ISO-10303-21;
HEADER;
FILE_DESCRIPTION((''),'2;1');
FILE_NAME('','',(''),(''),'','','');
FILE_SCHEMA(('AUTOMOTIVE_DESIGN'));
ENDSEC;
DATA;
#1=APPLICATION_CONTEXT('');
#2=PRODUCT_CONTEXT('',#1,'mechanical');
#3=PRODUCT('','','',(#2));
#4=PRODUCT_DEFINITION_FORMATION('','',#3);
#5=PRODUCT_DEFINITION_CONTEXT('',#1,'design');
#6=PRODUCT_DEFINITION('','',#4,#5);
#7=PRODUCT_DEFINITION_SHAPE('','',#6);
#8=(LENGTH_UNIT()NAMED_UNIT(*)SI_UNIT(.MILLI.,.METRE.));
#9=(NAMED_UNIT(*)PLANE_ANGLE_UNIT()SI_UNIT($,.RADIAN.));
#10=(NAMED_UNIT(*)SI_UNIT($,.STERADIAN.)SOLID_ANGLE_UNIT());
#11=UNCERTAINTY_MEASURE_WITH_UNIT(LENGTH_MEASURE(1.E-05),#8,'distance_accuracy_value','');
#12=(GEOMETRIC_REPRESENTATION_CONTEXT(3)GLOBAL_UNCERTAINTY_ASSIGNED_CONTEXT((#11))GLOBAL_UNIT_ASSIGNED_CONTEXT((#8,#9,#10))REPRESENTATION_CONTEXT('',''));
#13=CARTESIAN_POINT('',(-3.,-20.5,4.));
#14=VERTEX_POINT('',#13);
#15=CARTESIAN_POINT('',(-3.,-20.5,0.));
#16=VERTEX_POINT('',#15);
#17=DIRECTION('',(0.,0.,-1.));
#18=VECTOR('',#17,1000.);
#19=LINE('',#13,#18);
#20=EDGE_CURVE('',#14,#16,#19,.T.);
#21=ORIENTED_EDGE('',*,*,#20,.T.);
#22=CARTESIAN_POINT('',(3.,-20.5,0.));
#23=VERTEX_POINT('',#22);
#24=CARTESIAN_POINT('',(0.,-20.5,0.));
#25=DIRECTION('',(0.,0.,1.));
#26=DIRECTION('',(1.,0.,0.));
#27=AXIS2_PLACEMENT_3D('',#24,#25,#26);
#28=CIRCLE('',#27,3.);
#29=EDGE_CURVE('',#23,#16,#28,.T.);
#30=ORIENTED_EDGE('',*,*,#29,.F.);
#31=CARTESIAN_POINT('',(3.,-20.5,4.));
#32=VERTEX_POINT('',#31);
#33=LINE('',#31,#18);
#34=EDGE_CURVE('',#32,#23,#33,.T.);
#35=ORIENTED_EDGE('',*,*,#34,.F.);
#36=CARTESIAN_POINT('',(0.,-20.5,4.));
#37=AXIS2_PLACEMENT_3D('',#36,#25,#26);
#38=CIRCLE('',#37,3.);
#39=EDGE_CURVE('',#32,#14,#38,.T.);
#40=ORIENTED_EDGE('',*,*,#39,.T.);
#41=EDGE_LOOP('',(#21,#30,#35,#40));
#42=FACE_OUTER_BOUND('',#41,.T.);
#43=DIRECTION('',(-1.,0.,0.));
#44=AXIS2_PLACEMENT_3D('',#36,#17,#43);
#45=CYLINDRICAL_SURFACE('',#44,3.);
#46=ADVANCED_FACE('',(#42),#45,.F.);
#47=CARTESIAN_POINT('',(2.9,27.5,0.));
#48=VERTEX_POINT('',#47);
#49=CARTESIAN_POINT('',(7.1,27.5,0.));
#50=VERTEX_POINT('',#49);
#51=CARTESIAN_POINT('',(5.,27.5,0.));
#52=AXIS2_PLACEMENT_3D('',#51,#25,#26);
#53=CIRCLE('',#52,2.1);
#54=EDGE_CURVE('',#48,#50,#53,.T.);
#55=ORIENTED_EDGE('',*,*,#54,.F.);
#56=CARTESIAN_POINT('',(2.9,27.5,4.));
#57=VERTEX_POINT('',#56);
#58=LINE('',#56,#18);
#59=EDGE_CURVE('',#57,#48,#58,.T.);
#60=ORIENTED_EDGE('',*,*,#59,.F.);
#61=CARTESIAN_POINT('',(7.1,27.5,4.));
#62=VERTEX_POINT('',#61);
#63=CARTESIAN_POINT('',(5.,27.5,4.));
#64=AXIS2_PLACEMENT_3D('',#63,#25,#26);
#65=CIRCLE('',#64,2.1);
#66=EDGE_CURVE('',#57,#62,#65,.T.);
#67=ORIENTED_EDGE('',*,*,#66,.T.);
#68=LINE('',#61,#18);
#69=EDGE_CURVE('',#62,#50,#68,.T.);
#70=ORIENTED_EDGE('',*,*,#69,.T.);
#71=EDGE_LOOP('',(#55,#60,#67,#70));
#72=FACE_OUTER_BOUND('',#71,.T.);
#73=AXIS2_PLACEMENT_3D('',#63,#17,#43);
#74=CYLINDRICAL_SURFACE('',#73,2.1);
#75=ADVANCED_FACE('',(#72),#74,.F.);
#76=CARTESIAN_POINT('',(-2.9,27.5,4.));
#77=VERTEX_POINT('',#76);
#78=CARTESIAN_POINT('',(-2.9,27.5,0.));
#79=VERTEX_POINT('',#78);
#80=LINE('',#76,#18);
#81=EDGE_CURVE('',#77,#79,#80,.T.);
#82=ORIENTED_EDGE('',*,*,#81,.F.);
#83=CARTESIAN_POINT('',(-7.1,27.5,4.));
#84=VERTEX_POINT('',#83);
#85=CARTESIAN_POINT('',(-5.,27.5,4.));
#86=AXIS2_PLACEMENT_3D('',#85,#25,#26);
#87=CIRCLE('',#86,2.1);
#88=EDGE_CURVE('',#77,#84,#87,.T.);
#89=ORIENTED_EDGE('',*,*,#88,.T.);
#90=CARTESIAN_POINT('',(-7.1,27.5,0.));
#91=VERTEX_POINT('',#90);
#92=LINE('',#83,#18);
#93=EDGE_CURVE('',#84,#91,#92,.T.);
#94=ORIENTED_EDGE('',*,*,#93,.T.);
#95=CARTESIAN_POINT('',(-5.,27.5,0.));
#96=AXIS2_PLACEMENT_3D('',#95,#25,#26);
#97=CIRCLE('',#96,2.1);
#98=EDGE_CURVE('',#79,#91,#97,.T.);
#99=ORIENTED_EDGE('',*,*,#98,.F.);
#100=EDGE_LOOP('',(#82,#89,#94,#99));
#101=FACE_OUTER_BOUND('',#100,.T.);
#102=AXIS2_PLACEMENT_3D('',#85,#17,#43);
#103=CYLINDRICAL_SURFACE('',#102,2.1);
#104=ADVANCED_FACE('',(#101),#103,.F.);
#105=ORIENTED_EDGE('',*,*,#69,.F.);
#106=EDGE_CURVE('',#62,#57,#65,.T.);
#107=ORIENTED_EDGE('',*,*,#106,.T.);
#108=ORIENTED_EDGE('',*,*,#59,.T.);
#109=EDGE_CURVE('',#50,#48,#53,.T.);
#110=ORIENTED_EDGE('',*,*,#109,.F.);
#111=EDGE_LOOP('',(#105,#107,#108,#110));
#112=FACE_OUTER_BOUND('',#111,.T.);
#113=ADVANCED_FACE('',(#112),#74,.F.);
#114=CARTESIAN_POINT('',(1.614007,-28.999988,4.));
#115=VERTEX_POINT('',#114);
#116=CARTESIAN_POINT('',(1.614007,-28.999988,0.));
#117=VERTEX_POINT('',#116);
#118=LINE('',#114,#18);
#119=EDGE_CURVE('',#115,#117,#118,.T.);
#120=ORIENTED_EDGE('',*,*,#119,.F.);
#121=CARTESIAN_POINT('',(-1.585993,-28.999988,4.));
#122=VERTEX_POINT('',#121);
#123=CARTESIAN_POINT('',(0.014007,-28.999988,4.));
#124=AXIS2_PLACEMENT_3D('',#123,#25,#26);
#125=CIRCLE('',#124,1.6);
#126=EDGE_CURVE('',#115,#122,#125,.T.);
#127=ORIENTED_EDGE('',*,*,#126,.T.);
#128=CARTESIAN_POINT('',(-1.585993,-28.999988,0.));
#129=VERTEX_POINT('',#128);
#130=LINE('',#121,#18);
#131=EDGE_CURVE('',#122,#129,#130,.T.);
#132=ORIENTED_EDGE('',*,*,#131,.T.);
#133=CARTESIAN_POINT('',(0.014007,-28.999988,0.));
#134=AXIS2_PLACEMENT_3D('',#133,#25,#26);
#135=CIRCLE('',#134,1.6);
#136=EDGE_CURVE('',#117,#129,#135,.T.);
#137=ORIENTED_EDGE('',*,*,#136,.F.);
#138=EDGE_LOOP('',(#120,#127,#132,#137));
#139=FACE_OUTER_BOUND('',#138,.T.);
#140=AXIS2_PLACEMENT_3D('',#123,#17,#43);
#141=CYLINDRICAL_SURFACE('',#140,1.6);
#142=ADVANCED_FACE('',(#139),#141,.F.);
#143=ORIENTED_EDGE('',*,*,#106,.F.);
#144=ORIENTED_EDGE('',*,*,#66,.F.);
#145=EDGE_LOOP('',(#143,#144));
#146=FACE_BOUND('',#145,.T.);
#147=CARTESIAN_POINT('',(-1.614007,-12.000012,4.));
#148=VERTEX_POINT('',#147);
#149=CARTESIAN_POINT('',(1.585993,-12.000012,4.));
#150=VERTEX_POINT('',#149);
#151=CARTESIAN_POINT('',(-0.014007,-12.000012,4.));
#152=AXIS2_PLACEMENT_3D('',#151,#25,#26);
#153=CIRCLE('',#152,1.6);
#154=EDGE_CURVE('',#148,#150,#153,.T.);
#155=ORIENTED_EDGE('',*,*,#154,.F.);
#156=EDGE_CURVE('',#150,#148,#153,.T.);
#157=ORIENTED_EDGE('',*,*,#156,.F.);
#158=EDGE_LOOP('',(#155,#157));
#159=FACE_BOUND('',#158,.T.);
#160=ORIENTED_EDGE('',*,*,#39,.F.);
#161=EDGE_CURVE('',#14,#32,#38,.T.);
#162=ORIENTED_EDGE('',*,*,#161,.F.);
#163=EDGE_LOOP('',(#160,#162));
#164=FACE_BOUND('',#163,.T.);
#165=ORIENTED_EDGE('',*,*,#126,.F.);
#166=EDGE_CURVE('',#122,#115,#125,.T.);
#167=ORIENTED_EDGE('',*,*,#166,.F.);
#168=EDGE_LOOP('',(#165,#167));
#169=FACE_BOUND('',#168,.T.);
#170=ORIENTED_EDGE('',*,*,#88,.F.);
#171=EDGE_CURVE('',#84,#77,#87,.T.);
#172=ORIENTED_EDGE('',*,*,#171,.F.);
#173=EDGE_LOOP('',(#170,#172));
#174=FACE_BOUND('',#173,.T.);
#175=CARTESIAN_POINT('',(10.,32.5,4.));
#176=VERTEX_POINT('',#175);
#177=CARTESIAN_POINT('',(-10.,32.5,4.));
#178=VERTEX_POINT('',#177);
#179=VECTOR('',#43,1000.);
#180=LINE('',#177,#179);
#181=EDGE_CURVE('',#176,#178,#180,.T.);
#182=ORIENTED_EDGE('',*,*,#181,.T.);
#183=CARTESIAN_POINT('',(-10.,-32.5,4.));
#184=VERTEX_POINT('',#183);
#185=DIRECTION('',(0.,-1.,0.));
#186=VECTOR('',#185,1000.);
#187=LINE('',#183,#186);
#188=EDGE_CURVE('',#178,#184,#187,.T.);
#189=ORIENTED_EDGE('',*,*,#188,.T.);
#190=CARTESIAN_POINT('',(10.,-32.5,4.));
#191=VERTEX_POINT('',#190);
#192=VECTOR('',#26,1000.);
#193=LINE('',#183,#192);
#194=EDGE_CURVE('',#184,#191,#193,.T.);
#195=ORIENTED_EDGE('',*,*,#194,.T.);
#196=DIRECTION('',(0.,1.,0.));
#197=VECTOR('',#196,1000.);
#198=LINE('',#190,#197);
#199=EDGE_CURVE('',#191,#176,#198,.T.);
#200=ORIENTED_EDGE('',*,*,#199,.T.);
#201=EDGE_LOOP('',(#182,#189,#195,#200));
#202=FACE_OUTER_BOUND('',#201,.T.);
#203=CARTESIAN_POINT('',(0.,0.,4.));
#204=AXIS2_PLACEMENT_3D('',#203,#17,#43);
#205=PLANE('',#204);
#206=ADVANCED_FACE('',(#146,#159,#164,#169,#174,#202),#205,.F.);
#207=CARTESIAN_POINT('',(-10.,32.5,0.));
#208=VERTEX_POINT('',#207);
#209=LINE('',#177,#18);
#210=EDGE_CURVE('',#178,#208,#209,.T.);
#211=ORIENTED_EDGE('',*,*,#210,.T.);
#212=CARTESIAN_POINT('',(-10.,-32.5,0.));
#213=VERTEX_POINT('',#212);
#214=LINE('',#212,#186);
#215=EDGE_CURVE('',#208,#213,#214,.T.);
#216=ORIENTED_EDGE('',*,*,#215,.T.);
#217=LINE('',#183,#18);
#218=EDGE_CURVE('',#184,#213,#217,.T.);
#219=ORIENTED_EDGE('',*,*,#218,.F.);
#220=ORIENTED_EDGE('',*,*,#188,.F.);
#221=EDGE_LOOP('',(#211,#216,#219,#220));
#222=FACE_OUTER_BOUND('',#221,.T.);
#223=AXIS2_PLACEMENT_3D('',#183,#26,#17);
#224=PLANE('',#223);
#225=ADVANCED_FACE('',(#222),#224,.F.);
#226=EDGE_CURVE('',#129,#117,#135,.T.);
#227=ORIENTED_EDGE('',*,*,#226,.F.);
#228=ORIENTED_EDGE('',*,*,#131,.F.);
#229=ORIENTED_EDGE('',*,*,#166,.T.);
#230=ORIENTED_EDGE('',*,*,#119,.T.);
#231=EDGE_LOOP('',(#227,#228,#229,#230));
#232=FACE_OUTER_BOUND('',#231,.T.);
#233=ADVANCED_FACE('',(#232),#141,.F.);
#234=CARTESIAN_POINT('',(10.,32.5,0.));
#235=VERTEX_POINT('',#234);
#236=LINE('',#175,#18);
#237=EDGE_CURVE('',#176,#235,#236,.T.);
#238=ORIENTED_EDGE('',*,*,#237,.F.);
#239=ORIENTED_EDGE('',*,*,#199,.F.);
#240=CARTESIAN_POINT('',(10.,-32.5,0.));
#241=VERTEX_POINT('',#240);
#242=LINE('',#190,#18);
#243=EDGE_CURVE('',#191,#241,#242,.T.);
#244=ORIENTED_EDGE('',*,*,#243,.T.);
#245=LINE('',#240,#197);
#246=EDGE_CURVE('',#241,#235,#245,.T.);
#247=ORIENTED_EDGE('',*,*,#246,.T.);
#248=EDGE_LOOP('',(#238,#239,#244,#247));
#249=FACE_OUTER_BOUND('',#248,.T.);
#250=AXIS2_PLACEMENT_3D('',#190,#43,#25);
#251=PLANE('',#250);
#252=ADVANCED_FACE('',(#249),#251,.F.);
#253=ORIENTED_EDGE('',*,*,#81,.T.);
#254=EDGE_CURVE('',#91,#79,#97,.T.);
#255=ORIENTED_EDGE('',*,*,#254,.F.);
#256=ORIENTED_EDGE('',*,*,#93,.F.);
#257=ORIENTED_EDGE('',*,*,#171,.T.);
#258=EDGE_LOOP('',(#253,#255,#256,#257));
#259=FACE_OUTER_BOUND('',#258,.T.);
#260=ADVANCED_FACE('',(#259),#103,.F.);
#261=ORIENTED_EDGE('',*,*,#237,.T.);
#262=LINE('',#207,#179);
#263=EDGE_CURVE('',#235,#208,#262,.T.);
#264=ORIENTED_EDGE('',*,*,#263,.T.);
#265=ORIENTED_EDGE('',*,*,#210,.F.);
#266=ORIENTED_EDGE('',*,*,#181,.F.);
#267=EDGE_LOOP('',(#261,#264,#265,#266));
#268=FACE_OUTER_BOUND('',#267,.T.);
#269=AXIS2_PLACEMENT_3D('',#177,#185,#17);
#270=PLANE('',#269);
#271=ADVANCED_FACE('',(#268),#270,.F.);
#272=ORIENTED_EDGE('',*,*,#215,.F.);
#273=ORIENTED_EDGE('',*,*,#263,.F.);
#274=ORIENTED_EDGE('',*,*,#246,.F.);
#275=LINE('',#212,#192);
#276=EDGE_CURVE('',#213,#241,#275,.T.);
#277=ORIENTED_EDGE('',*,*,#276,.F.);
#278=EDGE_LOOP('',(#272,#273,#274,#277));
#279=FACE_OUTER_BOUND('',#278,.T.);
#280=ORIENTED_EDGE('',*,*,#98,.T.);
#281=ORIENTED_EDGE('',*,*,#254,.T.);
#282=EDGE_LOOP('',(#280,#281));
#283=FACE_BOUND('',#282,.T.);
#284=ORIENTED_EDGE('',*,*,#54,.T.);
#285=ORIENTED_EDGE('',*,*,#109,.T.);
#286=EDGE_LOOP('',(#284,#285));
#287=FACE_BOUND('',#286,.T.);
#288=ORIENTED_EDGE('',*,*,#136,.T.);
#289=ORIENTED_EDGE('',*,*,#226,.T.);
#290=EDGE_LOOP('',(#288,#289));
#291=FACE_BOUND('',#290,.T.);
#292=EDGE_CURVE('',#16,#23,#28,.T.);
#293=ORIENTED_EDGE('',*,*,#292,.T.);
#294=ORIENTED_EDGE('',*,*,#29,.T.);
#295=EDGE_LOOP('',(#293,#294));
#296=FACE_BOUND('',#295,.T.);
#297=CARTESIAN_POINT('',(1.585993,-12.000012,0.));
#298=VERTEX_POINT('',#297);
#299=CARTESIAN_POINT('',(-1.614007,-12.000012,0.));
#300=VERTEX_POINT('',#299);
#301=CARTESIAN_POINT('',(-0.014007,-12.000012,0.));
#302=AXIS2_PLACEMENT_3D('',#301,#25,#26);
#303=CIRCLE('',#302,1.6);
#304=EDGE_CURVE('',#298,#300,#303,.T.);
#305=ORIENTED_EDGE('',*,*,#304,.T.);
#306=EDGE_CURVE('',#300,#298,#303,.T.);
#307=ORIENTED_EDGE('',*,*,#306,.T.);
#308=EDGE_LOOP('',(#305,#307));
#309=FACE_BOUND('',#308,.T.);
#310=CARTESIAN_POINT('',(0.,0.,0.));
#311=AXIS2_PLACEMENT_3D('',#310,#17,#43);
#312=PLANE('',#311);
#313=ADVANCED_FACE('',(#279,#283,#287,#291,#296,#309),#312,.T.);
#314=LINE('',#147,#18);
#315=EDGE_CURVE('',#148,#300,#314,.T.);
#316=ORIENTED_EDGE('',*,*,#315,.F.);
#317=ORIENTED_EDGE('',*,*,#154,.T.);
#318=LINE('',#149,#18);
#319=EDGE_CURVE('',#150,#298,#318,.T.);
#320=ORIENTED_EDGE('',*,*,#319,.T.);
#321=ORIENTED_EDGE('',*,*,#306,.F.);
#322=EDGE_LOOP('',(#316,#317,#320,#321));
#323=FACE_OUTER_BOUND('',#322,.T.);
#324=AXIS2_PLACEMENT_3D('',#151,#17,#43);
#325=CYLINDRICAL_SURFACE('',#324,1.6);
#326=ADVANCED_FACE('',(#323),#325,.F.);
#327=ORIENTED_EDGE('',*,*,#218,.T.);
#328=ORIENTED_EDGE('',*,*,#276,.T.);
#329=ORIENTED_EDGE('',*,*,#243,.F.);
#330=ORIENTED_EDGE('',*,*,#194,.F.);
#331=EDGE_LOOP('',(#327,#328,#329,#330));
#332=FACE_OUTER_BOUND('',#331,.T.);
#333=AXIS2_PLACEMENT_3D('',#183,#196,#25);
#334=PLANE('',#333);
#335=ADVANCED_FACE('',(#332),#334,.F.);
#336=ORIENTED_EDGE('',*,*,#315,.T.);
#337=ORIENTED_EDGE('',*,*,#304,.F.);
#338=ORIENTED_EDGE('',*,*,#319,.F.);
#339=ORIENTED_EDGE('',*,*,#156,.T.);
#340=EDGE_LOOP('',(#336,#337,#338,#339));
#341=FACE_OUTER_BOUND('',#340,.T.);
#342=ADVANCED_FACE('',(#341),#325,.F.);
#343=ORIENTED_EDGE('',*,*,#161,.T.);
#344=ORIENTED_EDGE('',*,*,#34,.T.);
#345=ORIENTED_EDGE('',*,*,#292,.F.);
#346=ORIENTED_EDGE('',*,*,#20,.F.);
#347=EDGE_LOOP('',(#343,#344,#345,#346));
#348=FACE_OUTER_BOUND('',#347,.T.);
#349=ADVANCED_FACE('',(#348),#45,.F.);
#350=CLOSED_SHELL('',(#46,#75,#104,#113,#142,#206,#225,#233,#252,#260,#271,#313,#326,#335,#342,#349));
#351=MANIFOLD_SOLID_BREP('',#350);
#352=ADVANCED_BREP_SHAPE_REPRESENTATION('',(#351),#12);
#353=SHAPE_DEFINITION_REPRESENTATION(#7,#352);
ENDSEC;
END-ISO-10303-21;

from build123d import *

# Parameters (mm, degrees)
SKETCH1_W           = 20
SKETCH1_H           = 65
SKETCH1_R           = 2.1
SKETCH1_R_2         = 3
SKETCH1_R_3         = 1.6
BOSS_EXTRUDE1_DEPTH = 4


with BuildPart() as part:
    # Sketch1 → Boss-Extrude1 (new body)
    with BuildSketch(Plane.XY):
        Rectangle(SKETCH1_W, SKETCH1_H)
        with Locations((-5, 27.5)):
            Circle(SKETCH1_R, mode=Mode.SUBTRACT)
        with Locations((5, 27.5)):
            Circle(SKETCH1_R, mode=Mode.SUBTRACT)
        with Locations((0, -20.5)):
            Circle(SKETCH1_R_2, mode=Mode.SUBTRACT)
        with Locations((-0.014007289, -12.000011541)):
            Circle(SKETCH1_R_3, mode=Mode.SUBTRACT)
        with Locations((0.014007289, -28.999988459)):
            Circle(SKETCH1_R_3, mode=Mode.SUBTRACT)
    extrude(amount=BOSS_EXTRUDE1_DEPTH)


solid = part.part
